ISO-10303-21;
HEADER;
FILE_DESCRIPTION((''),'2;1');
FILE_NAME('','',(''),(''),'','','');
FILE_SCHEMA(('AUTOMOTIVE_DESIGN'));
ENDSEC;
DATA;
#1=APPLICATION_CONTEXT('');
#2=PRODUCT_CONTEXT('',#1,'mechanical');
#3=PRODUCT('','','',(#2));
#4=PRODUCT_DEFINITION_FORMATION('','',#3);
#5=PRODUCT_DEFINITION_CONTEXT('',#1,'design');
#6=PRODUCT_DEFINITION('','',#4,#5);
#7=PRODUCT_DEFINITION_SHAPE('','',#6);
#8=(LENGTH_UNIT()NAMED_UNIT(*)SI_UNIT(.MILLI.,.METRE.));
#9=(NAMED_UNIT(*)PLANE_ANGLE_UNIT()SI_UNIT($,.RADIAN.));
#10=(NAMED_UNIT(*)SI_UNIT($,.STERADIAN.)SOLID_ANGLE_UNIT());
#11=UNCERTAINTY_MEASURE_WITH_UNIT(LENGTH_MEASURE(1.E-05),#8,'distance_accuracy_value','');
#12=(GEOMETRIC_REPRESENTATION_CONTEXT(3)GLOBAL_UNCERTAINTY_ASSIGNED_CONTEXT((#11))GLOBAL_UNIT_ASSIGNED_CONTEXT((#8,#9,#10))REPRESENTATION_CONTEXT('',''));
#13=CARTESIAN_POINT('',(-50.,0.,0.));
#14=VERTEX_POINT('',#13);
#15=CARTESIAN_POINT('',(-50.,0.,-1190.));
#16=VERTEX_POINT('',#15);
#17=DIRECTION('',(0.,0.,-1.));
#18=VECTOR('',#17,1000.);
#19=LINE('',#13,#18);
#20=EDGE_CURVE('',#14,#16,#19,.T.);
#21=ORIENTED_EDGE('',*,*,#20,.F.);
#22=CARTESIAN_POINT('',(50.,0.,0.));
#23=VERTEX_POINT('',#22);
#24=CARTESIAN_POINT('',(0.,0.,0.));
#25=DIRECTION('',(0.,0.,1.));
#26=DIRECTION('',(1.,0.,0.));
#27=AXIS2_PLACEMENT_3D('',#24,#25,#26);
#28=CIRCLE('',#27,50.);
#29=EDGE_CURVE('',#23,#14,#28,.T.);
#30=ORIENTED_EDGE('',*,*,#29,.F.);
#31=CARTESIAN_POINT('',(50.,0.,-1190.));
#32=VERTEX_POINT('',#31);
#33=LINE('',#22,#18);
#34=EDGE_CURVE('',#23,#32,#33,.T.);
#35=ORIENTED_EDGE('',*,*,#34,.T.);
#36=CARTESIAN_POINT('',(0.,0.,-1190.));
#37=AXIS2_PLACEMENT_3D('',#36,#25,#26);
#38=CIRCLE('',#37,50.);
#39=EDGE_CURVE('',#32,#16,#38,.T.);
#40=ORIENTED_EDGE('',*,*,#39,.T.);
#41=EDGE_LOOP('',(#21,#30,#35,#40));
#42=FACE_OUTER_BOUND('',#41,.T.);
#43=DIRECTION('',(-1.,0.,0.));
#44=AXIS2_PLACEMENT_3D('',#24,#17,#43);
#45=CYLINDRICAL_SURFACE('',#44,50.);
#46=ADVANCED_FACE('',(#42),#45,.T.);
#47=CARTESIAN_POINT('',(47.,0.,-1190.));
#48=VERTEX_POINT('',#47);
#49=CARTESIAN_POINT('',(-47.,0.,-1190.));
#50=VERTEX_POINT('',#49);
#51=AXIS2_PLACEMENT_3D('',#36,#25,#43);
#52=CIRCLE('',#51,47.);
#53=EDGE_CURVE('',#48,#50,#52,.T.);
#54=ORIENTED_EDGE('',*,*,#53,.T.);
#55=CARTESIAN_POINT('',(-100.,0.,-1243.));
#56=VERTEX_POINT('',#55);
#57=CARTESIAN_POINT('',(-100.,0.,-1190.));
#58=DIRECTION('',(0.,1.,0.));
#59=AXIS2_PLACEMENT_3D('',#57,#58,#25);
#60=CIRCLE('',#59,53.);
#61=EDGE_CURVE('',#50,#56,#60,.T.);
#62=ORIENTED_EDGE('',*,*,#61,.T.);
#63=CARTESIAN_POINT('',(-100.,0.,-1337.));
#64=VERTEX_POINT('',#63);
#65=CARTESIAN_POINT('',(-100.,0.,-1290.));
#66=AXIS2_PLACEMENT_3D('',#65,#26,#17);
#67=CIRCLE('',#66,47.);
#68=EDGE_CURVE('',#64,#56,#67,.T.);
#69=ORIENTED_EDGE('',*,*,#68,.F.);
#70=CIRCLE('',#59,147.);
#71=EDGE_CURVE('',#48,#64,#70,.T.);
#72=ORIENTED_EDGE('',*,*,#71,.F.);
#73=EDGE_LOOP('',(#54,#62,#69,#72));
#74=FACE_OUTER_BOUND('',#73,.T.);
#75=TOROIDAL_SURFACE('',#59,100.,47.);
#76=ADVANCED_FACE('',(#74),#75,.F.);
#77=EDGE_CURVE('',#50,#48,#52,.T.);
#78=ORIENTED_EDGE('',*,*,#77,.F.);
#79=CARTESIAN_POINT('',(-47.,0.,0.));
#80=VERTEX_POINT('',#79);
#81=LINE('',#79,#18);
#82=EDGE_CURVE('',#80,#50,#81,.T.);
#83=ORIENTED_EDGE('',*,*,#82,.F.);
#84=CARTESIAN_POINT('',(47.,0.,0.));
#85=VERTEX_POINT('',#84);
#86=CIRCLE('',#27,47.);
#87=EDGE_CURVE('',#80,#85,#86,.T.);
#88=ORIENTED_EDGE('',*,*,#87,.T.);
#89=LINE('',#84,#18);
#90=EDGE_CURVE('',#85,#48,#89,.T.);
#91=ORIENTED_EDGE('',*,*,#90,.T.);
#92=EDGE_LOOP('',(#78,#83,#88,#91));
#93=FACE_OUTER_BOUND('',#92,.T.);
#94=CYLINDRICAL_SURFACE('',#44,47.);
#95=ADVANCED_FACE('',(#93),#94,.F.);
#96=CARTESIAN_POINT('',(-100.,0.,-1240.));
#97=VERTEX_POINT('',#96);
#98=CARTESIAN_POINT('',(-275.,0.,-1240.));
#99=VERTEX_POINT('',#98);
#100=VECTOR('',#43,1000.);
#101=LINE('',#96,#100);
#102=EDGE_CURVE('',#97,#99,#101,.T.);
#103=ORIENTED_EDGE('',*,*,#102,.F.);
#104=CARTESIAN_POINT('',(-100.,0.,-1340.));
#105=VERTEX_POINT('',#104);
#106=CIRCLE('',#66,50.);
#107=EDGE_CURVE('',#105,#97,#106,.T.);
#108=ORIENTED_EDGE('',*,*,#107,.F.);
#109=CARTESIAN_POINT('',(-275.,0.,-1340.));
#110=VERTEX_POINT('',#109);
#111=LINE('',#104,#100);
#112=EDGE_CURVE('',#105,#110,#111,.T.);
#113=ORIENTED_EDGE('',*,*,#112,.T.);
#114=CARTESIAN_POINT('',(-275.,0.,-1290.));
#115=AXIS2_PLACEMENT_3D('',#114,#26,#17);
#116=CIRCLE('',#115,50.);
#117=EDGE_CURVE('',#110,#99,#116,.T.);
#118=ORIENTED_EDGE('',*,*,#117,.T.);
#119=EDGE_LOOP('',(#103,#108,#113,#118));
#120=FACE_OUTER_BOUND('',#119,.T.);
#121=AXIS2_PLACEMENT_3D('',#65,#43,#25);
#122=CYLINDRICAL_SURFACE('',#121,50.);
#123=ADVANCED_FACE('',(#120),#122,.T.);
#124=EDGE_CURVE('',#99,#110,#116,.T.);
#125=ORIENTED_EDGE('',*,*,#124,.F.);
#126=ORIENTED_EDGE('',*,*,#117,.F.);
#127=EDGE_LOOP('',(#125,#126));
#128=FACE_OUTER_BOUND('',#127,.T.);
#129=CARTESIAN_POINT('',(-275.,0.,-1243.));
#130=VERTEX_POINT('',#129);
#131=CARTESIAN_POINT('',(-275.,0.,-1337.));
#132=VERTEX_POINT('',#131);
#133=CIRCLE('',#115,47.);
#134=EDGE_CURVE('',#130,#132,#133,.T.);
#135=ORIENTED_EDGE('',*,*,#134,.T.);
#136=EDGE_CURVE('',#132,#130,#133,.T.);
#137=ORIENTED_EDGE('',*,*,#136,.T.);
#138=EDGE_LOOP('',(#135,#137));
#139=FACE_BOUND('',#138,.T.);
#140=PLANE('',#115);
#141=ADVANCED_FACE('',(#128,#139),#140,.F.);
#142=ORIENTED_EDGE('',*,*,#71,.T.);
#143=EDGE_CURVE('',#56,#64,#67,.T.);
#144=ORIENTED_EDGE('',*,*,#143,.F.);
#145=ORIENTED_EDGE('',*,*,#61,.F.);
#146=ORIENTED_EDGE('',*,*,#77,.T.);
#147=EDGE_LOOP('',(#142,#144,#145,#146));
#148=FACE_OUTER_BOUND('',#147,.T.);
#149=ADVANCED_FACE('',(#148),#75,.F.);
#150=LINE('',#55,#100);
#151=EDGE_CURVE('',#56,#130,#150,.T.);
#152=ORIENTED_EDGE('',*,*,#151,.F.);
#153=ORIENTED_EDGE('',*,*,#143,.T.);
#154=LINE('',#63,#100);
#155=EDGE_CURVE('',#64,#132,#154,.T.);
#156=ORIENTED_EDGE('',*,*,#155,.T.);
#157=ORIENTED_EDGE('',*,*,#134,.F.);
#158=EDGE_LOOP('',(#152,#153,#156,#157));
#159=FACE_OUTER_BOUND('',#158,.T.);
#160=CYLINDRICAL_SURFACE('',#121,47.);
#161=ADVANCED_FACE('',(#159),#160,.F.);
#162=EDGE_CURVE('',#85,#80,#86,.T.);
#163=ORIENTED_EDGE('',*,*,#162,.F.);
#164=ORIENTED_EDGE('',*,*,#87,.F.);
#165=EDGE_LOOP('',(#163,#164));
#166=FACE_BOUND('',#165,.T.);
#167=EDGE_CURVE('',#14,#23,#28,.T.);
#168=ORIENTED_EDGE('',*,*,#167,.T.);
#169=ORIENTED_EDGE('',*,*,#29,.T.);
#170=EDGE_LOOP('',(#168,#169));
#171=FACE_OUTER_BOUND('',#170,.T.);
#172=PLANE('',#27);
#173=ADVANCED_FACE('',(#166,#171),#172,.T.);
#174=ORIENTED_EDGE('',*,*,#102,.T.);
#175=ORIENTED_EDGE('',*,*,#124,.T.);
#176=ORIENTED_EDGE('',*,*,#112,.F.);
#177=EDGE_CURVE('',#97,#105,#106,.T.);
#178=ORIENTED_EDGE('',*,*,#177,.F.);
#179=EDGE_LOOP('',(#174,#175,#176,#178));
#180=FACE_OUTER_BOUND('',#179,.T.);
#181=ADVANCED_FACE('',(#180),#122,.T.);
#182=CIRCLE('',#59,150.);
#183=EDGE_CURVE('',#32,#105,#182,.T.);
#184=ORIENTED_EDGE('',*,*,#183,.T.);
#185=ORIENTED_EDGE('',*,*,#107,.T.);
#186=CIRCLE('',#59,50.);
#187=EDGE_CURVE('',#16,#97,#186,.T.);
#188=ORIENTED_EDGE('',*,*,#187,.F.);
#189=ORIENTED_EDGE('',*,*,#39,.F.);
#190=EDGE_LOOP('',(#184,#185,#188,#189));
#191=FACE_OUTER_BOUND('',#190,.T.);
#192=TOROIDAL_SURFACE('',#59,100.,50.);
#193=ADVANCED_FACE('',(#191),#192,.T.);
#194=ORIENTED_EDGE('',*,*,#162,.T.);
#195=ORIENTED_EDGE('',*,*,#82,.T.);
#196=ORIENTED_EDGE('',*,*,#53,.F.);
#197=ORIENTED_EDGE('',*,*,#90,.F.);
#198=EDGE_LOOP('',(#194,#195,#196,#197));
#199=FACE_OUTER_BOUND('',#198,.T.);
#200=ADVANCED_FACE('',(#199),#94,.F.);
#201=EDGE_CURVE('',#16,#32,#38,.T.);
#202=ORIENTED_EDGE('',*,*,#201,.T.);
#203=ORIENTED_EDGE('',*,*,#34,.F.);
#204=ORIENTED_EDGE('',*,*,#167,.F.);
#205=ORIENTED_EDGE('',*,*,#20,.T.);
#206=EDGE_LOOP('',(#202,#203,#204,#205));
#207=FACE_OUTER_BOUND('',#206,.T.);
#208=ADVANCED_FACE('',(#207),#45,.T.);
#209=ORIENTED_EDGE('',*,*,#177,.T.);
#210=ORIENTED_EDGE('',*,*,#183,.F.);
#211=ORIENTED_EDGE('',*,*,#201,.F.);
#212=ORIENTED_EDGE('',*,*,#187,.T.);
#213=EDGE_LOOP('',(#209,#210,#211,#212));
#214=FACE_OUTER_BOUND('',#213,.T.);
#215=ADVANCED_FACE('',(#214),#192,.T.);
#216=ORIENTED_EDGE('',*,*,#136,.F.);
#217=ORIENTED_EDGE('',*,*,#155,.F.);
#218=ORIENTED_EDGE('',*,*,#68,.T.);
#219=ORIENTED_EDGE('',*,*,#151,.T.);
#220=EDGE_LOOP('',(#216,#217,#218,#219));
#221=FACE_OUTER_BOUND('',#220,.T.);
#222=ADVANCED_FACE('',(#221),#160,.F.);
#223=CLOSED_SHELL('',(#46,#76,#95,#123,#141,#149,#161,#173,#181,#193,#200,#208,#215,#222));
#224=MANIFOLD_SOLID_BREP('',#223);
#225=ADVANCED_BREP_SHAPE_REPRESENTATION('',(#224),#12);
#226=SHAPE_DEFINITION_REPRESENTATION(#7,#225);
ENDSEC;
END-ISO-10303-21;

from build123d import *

# Parameters (mm, degrees)
SKETCH_1_R = 50
SHELL_1_T  = -3


with BuildPart() as part:
    # 扫描1: sweep along a path in 草图2
    with BuildLine(Plane(origin=(0, 0, 0), x_dir=(1, 0, 0), z_dir=(0, 1, 0))) as sweep_1_path:
        Line((0, 0), (0, 1190))
        ThreePointArc((0, 1190), (-29.289321881, 1260.710678119), (-100, 1290))
        Line((-100, 1290), (-275, 1290))
    # 草图1 → 扫描1 (sweep)
    with BuildSketch(Plane.XY):
        Circle(SKETCH_1_R)
    sweep(path=sweep_1_path.line)

    # 抽壳1
    shell_1_openings = [part.faces().sort_by_distance(p)[0] for p in [
        (-275, 0, -1290),
        (0, 0, 0),
    ]]
    offset(amount=SHELL_1_T, openings=shell_1_openings, kind=Kind.INTERSECTION)


solid = part.part
